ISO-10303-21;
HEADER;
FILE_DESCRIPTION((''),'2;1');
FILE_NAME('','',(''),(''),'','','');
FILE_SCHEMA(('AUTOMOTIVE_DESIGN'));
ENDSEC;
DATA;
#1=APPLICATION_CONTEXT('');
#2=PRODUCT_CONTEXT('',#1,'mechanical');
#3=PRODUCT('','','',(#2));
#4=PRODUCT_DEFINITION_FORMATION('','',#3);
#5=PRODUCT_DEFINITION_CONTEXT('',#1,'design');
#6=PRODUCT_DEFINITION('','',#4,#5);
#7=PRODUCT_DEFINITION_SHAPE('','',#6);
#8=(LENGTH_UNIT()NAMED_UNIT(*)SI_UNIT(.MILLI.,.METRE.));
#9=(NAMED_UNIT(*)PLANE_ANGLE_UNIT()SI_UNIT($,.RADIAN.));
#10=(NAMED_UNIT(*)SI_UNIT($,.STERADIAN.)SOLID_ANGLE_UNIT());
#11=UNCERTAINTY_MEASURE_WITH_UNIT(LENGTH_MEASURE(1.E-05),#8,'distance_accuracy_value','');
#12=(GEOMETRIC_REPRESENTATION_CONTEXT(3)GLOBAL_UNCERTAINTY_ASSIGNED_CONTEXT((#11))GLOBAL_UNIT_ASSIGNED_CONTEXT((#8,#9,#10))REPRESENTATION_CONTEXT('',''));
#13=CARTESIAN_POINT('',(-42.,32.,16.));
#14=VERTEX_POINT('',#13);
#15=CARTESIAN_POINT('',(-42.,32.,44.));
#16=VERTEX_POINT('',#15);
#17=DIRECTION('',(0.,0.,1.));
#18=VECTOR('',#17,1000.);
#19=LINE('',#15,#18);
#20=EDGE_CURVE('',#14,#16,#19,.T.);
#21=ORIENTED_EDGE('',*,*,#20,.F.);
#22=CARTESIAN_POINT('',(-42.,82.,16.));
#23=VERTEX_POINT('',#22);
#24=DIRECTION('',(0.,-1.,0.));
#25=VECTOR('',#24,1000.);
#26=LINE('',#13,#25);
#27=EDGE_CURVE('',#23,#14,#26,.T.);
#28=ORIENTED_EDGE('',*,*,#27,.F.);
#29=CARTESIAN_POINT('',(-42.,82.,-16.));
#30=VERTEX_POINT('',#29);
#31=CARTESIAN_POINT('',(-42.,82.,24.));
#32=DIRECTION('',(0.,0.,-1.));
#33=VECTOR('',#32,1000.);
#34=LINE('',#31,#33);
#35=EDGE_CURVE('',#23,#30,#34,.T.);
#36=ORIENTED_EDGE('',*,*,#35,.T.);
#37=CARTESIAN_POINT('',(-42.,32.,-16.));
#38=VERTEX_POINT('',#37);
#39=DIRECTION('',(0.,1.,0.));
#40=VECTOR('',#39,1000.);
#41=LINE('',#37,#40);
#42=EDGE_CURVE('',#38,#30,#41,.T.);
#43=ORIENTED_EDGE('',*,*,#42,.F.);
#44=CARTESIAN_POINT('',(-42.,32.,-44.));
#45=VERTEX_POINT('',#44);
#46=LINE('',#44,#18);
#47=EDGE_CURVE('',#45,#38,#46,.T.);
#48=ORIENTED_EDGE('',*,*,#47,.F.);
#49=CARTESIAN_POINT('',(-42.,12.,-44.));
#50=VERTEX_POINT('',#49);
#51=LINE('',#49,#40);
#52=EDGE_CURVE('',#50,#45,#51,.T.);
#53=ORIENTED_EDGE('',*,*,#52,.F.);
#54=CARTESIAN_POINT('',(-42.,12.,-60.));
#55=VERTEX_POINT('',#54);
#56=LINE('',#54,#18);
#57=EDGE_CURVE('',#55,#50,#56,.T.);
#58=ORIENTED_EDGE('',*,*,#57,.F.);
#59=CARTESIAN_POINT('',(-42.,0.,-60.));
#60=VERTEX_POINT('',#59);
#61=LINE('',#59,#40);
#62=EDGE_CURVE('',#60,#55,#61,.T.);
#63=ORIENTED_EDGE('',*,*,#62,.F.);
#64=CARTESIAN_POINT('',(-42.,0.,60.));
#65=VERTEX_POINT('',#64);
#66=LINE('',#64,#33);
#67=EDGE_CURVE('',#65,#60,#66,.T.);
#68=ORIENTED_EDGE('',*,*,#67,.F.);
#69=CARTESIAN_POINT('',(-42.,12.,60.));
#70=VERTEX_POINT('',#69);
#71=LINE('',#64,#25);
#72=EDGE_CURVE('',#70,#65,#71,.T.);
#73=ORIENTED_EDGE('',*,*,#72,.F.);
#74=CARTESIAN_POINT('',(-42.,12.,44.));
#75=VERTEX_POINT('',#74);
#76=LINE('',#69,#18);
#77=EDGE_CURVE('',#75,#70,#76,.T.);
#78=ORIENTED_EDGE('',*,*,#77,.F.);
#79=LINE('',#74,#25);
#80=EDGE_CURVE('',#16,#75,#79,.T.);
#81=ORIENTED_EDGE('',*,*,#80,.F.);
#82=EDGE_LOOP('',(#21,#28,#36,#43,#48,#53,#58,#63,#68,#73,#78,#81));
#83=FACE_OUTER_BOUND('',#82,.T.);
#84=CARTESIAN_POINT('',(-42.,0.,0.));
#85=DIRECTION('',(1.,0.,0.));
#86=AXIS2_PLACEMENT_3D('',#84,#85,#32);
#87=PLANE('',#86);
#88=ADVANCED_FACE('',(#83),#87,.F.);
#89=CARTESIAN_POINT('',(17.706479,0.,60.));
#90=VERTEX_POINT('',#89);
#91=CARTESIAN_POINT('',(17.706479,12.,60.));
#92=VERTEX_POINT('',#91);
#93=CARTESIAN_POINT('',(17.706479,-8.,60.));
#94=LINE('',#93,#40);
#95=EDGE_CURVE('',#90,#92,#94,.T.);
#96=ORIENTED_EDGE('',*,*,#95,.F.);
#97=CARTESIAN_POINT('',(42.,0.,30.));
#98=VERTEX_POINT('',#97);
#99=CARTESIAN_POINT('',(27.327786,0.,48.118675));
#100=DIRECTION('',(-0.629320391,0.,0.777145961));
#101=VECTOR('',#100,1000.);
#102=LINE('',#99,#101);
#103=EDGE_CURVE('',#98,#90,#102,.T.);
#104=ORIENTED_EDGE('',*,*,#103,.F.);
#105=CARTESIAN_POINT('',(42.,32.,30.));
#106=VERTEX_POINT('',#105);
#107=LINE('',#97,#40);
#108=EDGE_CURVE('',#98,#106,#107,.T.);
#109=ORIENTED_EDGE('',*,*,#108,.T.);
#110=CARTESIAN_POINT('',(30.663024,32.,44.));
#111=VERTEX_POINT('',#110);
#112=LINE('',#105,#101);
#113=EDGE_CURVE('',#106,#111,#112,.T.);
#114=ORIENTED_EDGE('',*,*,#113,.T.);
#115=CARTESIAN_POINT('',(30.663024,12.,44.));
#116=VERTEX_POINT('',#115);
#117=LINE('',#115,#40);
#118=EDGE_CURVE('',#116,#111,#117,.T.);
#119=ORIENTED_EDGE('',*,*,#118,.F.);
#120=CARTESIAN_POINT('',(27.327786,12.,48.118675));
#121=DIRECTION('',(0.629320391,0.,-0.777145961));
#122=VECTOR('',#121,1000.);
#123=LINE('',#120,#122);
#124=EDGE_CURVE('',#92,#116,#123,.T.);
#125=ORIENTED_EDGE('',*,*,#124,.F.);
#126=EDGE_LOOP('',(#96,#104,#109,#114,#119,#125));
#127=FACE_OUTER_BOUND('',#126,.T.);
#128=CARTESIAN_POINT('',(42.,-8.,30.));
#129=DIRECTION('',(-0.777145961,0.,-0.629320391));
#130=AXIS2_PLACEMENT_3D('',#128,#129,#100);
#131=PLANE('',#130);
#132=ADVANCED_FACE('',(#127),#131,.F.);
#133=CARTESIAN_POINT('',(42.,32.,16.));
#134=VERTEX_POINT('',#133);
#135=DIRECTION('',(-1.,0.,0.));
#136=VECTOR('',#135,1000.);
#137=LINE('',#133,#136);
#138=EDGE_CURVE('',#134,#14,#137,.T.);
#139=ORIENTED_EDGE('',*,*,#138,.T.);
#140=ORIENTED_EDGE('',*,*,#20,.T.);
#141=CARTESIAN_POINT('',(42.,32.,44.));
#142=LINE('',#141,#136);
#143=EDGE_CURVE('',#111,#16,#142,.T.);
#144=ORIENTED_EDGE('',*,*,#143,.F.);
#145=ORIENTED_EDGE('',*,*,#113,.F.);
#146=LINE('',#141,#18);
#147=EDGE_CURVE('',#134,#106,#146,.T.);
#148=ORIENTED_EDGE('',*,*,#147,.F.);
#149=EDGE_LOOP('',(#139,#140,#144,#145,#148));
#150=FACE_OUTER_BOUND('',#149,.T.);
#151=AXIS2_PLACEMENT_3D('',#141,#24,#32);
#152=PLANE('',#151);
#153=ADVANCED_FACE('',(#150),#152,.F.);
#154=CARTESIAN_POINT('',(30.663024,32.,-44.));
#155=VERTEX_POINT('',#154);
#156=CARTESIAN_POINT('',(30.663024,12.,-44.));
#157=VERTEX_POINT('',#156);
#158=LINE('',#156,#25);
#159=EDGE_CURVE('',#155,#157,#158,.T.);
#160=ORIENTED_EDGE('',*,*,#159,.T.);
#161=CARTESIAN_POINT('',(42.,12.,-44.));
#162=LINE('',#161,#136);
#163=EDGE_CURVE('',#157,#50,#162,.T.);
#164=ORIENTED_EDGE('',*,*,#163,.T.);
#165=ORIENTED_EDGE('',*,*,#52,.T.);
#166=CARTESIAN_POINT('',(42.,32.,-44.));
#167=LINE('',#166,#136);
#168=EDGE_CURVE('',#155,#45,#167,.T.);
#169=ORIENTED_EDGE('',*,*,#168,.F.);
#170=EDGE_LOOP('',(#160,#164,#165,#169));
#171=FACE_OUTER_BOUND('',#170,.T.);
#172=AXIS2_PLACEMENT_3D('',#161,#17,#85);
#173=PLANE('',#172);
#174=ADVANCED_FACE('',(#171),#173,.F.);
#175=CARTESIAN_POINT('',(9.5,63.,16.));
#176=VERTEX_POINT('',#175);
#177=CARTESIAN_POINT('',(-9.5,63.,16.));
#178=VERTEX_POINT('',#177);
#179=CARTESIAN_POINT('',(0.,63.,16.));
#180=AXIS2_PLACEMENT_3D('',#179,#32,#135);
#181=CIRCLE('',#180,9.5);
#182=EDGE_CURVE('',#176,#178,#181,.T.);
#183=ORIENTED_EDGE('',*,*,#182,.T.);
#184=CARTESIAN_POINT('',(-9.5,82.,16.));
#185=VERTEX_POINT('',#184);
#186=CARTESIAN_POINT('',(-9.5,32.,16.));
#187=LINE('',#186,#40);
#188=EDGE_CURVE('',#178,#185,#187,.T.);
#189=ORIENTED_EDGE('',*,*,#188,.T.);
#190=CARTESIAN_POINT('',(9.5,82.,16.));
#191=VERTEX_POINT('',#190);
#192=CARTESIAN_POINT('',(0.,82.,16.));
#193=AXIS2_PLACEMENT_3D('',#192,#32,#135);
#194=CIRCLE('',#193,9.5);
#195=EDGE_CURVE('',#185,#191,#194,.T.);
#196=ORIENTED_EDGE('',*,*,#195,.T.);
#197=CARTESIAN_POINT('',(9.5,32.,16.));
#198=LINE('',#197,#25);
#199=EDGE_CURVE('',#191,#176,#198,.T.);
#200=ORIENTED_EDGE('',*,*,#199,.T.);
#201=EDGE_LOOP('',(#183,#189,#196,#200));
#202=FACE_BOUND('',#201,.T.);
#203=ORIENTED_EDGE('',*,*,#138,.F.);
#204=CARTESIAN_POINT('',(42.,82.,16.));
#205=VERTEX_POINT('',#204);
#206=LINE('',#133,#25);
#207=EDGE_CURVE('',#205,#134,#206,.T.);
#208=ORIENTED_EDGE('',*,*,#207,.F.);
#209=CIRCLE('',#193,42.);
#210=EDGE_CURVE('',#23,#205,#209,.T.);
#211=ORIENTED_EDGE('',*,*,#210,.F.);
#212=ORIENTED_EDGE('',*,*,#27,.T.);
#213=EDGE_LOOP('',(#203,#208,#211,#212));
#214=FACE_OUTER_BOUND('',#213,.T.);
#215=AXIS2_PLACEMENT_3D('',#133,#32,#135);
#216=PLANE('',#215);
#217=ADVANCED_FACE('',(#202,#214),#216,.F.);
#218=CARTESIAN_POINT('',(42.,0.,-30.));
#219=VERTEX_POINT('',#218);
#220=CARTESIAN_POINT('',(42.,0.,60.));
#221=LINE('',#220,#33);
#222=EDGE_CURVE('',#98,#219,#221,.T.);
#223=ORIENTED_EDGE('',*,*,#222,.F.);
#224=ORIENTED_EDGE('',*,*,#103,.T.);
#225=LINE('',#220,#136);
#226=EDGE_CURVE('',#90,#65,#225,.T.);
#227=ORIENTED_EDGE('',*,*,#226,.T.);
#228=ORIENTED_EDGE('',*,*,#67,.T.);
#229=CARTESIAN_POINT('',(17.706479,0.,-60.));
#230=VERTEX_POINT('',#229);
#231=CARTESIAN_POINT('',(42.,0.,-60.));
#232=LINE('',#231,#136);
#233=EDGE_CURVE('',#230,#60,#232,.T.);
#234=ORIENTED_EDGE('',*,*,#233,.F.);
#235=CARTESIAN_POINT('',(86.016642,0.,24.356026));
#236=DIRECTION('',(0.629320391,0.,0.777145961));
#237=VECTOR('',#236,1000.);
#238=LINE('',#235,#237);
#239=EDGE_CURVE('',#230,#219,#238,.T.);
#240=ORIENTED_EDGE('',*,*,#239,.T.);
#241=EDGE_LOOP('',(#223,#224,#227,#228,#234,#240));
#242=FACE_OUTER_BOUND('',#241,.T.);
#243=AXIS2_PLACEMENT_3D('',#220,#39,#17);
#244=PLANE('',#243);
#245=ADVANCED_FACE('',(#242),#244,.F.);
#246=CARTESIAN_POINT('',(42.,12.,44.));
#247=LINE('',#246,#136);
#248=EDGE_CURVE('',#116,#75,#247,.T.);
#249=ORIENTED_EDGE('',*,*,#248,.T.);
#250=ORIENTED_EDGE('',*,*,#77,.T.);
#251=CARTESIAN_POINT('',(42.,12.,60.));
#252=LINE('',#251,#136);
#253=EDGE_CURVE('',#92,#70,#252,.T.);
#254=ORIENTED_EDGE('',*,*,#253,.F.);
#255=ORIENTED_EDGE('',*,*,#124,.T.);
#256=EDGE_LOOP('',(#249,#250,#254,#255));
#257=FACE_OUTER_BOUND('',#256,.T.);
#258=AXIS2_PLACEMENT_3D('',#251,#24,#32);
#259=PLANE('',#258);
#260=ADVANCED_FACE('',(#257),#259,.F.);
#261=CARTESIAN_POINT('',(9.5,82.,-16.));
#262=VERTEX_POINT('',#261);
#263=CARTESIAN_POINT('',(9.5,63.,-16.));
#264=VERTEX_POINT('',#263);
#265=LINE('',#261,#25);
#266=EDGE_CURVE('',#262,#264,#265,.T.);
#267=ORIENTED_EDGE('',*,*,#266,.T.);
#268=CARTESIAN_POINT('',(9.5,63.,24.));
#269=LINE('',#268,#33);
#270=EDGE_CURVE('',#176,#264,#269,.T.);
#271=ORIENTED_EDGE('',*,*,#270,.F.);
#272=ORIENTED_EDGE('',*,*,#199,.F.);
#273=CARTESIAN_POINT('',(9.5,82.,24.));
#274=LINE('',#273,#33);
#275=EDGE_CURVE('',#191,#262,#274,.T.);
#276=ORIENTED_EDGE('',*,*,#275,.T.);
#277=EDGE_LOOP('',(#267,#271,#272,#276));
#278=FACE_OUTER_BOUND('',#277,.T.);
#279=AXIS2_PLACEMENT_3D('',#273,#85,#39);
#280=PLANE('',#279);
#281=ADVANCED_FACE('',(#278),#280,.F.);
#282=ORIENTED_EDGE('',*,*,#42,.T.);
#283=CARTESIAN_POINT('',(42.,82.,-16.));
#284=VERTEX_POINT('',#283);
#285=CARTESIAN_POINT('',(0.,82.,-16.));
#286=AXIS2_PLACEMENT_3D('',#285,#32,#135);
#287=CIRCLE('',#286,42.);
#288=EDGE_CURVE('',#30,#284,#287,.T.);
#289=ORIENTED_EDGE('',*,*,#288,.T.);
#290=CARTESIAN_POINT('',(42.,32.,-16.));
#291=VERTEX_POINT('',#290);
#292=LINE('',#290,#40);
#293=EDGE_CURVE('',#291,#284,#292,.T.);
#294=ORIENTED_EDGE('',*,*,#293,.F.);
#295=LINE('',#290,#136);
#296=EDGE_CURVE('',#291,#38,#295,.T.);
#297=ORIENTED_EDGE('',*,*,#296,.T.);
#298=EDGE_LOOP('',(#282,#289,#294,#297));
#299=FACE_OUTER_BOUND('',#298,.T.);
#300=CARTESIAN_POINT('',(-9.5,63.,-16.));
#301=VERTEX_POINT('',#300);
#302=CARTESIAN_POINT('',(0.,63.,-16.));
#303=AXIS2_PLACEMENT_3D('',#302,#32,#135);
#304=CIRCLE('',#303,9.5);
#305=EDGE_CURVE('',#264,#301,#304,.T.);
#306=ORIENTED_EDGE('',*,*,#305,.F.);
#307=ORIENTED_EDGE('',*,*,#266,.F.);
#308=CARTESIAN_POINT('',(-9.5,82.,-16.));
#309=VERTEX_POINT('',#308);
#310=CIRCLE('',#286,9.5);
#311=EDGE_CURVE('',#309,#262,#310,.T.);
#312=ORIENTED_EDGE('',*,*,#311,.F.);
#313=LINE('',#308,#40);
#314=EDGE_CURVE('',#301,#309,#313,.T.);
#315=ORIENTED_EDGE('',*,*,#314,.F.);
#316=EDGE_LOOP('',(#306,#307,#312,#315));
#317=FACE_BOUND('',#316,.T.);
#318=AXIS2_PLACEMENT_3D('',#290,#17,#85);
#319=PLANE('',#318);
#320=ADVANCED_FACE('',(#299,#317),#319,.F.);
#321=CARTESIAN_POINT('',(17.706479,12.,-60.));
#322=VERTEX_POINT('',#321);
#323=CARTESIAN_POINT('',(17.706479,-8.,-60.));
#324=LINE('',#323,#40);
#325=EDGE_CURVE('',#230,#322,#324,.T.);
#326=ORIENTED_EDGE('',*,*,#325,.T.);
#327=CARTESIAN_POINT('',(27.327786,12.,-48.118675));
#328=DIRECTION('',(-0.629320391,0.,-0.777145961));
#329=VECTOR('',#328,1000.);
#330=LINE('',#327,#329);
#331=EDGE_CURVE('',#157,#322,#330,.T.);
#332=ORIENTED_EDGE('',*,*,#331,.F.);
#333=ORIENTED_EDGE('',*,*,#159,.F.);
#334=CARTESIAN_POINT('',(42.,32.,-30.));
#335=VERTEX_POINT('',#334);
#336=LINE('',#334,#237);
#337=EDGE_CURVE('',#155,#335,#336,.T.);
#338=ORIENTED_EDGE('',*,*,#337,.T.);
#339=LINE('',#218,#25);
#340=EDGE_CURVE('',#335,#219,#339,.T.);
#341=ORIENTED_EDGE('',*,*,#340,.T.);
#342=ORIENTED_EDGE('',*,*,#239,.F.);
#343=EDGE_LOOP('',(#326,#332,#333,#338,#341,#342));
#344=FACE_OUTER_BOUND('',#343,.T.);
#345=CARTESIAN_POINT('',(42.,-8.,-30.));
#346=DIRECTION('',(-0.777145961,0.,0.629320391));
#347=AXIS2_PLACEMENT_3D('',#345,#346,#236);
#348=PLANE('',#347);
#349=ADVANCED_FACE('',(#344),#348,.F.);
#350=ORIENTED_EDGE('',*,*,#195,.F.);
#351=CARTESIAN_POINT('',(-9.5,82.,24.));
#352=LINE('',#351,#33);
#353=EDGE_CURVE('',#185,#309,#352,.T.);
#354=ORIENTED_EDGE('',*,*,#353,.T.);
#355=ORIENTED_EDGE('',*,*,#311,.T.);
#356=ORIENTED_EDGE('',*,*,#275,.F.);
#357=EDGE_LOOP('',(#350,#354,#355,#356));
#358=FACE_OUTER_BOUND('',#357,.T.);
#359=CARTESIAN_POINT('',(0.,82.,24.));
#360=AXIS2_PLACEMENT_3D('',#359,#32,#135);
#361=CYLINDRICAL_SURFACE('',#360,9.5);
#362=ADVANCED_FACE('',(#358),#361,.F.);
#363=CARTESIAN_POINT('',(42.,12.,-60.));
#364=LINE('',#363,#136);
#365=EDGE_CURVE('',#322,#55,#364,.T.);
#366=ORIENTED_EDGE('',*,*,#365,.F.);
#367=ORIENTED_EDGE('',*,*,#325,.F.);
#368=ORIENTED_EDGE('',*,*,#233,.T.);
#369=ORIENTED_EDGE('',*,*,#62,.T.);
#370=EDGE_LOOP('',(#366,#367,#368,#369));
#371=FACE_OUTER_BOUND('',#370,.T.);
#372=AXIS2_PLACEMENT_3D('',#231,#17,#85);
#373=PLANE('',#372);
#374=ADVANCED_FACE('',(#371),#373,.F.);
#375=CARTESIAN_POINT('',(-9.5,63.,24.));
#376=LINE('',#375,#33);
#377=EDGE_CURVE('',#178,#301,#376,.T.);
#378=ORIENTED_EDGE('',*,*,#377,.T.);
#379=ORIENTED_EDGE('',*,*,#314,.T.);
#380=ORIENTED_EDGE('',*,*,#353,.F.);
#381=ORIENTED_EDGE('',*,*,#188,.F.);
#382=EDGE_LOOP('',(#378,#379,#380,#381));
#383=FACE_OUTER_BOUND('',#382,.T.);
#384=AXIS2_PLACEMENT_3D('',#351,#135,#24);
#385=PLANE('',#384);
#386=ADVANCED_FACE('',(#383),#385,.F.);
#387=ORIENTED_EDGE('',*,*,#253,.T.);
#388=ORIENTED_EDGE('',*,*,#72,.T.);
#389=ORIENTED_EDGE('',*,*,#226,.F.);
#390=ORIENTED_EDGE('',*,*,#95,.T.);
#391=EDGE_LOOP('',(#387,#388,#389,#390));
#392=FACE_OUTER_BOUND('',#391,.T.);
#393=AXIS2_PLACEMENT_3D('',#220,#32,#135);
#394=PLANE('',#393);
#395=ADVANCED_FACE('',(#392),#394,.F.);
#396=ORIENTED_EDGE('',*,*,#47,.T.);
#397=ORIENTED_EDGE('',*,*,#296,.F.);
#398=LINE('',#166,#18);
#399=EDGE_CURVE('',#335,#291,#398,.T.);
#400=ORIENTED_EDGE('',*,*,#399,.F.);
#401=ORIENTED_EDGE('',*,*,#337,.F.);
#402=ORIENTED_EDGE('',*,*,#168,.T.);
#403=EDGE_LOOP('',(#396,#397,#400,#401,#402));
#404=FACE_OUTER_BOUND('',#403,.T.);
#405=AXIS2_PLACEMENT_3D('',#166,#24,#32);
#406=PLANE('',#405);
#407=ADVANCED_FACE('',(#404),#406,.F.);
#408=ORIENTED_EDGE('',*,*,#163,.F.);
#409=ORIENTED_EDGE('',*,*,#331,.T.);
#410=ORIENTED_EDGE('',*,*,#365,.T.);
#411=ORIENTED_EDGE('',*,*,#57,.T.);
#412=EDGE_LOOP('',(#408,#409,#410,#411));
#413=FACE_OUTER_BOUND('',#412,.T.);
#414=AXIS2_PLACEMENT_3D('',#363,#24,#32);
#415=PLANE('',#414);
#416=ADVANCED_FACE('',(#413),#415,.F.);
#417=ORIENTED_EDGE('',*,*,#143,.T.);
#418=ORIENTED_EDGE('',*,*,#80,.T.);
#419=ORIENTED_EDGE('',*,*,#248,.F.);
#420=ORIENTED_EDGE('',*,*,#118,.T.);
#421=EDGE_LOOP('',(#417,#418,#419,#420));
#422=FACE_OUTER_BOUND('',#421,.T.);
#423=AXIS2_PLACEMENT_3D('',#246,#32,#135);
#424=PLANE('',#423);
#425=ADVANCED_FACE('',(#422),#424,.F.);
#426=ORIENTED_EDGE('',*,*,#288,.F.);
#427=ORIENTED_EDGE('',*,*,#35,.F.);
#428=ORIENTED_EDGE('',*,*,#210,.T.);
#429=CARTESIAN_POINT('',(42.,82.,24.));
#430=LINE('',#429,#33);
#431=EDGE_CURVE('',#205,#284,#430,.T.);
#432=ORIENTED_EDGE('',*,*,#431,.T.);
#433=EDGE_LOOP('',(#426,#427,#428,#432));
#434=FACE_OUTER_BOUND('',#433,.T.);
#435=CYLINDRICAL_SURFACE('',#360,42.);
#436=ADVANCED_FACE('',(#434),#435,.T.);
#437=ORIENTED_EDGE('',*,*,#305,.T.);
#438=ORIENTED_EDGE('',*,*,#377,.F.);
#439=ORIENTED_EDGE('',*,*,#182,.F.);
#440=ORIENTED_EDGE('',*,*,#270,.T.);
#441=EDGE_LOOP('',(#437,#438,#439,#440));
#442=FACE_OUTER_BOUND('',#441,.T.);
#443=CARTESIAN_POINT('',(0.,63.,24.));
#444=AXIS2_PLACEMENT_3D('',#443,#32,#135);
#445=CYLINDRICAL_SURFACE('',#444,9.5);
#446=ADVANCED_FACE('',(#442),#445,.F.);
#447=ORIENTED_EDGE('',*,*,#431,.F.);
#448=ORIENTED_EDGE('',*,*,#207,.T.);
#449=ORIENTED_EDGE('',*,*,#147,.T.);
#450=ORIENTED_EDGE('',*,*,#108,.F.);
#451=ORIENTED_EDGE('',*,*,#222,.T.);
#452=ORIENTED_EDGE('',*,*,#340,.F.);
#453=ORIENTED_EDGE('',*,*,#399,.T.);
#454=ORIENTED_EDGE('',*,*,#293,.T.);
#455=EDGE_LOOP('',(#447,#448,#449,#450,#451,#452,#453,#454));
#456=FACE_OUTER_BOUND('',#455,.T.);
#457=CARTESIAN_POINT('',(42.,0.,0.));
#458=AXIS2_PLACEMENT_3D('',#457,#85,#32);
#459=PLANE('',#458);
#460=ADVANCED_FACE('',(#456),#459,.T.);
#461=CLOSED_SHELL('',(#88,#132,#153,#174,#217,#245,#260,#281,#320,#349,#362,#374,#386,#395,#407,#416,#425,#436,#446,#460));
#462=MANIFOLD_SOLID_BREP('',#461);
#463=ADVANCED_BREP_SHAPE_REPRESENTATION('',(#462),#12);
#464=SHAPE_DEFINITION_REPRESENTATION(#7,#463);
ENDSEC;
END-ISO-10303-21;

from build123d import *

# Parameters (mm, degrees)
BRACKET_BODY_DEPTH            = 42
UPRIGHT_PROFILE_CUT_DEPTH     = 40
GUIDE_SLOT_DEPTH              = 40
ANGLED_CORNER_CUT_39DEG_DEPTH = 40


with BuildPart() as part:
    # Bracket Side Profile Sketch → Bracket Body (new, symmetric)
    with BuildSketch(Plane(origin=(0, 0, 0), x_dir=(0, 0, -1), z_dir=(1, 0, 0))):
        Polygon((-60, 0), (60, 0), (60, 12), (44, 12), (44, 32), (16, 32), (16, 124), (-16, 124), (-16, 32), (-44, 32), (-44, 12), (-60, 12), align=None)
    extrude(amount=BRACKET_BODY_DEPTH, both=True)

    # Upright Profile Cut Sketch → Upright Profile Cut (cut)
    with BuildSketch(Plane(origin=(0, 0, -16), x_dir=(-1, 0, 0), z_dir=(0, 0, -1))):
        with BuildLine():
            Line((-42, 124), (-42, 82))
            ThreePointArc((-42, 82), (-29.69848481, 111.69848481), (0, 124))
            Line((0, 124), (-42, 124))
        make_face()
        with BuildLine():
            Line((42, 124), (0, 124))
            ThreePointArc((0, 124), (29.69848481, 111.69848481), (42, 82))
            Line((42, 82), (42, 124))
        make_face()
    extrude(amount=-UPRIGHT_PROFILE_CUT_DEPTH, mode=Mode.SUBTRACT)

    # Guide Slot Sketch → Guide Slot (cut)
    with BuildSketch(Plane(origin=(0, 0, -16), x_dir=(-1, 0, 0), z_dir=(0, 0, -1))):
        with BuildLine():
            Line((9.5, 82), (9.5, 63))
            ThreePointArc((9.5, 63), (0, 53.5), (-9.5, 63))
            Line((-9.5, 63), (-9.5, 82))
            ThreePointArc((-9.5, 82), (0, 91.5), (9.5, 82))
        make_face()
    extrude(amount=-GUIDE_SLOT_DEPTH, mode=Mode.SUBTRACT)

    # Angled Corner Cut Sketch 39deg → Angled Corner Cut 39deg (cut)
    with BuildSketch(Plane(origin=(0, 32, 0), x_dir=(1, 0, 0), z_dir=(0, 1, 0))):
        Polygon((42, 30), (17.706479004, 60), (42, 60), align=None)
        Polygon((42, -60), (42, -30), (17.706479004, -60), align=None)
    extrude(amount=-ANGLED_CORNER_CUT_39DEG_DEPTH, mode=Mode.SUBTRACT)


solid = part.part
